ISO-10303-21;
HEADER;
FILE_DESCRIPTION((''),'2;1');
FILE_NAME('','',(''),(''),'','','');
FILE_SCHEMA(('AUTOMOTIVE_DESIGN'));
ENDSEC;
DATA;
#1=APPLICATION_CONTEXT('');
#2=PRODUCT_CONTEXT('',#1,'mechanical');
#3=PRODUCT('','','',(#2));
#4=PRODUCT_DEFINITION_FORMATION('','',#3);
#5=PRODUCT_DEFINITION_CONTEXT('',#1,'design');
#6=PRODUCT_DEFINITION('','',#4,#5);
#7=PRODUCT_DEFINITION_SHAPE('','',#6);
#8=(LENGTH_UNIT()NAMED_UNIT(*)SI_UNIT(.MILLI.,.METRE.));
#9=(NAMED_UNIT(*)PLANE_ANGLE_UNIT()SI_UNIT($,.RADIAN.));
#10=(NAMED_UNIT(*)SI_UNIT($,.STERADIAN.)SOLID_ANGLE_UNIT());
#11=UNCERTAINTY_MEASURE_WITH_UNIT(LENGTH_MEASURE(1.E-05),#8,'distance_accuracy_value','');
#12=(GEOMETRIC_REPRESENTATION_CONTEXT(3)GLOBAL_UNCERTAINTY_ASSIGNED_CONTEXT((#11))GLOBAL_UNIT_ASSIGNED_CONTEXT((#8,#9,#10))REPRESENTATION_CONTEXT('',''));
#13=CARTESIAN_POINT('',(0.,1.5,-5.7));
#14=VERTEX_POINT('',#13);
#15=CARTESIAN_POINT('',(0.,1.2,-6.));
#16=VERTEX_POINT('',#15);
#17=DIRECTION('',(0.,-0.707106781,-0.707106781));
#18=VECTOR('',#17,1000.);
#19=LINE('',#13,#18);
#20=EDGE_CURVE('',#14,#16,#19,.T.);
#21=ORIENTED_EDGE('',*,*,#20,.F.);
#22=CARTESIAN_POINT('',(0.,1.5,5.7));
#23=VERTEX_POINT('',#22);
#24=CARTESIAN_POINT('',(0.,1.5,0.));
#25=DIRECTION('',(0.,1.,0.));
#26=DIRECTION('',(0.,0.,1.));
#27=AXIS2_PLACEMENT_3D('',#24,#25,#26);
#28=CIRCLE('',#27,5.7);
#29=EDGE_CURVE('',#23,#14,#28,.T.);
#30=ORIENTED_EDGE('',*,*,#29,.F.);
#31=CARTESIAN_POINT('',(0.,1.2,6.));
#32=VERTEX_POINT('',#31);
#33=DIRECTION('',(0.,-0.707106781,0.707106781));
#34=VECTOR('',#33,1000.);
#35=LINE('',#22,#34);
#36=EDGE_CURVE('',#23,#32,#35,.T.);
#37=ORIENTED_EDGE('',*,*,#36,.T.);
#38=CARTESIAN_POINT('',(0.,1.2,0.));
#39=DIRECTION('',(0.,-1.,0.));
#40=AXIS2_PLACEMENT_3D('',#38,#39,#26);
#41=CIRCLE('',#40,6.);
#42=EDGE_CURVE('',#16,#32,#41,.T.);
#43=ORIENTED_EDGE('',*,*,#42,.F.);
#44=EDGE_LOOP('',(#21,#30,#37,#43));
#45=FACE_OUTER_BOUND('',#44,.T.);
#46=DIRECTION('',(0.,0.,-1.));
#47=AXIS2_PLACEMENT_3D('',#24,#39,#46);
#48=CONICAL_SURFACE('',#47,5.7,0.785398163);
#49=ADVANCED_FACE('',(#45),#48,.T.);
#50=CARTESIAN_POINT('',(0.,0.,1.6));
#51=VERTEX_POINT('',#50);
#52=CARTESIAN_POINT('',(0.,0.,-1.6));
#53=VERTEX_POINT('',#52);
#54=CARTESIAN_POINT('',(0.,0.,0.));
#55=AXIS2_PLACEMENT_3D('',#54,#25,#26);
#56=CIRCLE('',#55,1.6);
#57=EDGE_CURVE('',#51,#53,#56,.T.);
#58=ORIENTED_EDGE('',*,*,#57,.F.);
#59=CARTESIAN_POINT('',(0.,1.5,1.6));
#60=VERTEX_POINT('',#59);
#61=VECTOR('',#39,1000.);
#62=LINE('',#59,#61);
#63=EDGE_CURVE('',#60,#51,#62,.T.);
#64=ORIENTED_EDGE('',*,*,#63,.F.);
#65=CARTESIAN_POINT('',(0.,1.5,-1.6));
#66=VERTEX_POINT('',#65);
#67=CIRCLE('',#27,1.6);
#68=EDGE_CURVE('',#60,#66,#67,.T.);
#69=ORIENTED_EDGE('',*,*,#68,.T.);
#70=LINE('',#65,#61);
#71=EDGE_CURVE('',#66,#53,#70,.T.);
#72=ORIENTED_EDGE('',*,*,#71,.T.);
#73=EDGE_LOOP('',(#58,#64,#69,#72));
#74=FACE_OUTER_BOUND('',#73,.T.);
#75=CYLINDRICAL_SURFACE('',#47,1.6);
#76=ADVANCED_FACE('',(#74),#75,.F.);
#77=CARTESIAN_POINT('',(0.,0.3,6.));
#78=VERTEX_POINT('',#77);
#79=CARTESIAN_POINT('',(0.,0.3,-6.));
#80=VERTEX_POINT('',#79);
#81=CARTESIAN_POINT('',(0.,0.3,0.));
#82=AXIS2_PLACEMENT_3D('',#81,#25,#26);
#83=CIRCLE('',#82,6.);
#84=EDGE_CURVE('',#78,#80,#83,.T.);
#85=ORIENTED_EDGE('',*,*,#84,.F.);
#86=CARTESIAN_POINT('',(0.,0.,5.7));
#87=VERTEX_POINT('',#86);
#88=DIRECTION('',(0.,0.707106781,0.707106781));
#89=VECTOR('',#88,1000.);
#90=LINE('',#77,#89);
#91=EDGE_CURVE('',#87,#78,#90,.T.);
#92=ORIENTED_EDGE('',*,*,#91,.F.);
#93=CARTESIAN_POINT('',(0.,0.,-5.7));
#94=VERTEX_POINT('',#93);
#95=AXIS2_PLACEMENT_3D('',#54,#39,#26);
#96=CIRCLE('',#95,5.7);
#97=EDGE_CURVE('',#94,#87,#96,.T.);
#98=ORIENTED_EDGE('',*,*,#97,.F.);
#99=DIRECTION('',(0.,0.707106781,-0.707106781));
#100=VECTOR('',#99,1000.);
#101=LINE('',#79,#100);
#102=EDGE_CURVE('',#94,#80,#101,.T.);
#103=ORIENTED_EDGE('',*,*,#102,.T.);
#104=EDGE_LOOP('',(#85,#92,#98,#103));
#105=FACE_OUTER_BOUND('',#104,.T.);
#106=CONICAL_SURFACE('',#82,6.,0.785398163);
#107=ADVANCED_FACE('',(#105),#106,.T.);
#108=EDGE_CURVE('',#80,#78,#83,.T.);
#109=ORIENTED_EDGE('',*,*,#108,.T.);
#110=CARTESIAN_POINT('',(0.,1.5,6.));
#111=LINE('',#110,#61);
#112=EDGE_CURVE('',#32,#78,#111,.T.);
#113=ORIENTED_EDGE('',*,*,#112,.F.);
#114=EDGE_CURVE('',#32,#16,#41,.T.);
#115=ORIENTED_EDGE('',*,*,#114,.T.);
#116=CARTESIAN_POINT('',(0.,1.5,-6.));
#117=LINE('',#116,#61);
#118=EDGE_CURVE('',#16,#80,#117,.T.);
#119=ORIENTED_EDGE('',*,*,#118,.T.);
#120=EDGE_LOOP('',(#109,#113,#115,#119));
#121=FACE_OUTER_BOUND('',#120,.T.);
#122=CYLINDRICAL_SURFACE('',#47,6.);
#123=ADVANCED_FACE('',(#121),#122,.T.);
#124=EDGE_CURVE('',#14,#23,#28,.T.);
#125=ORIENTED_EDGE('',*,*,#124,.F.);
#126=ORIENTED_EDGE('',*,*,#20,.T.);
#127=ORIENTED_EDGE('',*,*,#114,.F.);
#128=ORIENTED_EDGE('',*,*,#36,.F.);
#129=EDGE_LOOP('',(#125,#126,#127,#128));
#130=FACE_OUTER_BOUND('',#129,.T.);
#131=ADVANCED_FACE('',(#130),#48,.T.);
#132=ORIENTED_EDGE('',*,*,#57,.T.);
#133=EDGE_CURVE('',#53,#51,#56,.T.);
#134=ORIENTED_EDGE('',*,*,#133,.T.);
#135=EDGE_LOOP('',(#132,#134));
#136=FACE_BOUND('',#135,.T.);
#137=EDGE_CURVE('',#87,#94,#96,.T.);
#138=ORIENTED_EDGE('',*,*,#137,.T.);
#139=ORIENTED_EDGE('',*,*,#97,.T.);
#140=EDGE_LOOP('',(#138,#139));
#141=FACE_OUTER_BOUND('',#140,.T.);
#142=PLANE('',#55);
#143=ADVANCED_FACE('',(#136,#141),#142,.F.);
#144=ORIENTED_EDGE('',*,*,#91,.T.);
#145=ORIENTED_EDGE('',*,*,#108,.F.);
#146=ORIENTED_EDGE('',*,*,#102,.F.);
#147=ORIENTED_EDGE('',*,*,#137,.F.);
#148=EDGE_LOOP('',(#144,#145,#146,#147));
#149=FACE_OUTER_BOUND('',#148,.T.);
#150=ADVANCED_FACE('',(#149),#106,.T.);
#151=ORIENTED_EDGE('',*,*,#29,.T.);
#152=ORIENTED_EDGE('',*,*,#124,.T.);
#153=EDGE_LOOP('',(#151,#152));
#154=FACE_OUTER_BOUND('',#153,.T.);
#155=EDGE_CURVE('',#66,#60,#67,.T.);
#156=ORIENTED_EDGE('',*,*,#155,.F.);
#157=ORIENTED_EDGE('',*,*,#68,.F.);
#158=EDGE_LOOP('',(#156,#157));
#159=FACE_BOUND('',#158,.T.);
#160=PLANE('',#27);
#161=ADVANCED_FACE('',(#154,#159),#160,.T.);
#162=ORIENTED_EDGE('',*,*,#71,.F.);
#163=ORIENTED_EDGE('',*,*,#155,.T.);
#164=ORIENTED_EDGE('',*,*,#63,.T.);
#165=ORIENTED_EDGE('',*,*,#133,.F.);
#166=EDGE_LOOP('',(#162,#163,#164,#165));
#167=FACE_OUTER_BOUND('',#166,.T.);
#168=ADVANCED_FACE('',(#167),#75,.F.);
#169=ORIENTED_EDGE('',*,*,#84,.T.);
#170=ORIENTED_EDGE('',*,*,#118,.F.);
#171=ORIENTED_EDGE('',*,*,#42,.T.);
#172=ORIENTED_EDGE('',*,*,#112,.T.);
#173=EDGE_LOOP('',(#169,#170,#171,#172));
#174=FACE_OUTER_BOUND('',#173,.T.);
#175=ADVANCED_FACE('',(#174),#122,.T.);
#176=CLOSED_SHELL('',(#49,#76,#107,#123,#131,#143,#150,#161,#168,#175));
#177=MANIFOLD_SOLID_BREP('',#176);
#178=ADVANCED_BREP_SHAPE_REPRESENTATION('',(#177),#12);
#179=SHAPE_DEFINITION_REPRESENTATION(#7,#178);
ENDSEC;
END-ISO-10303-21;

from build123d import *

# Parameters (mm, degrees)
SKETCH1_R           = 6
SKETCH1_R_2         = 1.6
BOSS_EXTRUDE1_DEPTH = 1.5
CHAMFER1_SIZE       = 0.3


with BuildPart() as part:
    # Sketch1 → Boss-Extrude1 (new body)
    with BuildSketch(Plane(origin=(0, 0, 0), x_dir=(1, 0, 0), z_dir=(0, 1, 0))):
        with Locations(Location((0, 0, 0), (0, 0, 270))):
            Circle(SKETCH1_R)
        with Locations(Location((0, 0, 0), (0, 0, 270))):
            Circle(SKETCH1_R_2, mode=Mode.SUBTRACT)
    extrude(amount=BOSS_EXTRUDE1_DEPTH)

    # Chamfer1
    chamfer1_edges = [part.edges().sort_by_distance(p)[0] for p in [
        (0, 0, -6),
        (0, 1.5, -6),
    ]]
    chamfer(chamfer1_edges, length=CHAMFER1_SIZE)


solid = part.part
